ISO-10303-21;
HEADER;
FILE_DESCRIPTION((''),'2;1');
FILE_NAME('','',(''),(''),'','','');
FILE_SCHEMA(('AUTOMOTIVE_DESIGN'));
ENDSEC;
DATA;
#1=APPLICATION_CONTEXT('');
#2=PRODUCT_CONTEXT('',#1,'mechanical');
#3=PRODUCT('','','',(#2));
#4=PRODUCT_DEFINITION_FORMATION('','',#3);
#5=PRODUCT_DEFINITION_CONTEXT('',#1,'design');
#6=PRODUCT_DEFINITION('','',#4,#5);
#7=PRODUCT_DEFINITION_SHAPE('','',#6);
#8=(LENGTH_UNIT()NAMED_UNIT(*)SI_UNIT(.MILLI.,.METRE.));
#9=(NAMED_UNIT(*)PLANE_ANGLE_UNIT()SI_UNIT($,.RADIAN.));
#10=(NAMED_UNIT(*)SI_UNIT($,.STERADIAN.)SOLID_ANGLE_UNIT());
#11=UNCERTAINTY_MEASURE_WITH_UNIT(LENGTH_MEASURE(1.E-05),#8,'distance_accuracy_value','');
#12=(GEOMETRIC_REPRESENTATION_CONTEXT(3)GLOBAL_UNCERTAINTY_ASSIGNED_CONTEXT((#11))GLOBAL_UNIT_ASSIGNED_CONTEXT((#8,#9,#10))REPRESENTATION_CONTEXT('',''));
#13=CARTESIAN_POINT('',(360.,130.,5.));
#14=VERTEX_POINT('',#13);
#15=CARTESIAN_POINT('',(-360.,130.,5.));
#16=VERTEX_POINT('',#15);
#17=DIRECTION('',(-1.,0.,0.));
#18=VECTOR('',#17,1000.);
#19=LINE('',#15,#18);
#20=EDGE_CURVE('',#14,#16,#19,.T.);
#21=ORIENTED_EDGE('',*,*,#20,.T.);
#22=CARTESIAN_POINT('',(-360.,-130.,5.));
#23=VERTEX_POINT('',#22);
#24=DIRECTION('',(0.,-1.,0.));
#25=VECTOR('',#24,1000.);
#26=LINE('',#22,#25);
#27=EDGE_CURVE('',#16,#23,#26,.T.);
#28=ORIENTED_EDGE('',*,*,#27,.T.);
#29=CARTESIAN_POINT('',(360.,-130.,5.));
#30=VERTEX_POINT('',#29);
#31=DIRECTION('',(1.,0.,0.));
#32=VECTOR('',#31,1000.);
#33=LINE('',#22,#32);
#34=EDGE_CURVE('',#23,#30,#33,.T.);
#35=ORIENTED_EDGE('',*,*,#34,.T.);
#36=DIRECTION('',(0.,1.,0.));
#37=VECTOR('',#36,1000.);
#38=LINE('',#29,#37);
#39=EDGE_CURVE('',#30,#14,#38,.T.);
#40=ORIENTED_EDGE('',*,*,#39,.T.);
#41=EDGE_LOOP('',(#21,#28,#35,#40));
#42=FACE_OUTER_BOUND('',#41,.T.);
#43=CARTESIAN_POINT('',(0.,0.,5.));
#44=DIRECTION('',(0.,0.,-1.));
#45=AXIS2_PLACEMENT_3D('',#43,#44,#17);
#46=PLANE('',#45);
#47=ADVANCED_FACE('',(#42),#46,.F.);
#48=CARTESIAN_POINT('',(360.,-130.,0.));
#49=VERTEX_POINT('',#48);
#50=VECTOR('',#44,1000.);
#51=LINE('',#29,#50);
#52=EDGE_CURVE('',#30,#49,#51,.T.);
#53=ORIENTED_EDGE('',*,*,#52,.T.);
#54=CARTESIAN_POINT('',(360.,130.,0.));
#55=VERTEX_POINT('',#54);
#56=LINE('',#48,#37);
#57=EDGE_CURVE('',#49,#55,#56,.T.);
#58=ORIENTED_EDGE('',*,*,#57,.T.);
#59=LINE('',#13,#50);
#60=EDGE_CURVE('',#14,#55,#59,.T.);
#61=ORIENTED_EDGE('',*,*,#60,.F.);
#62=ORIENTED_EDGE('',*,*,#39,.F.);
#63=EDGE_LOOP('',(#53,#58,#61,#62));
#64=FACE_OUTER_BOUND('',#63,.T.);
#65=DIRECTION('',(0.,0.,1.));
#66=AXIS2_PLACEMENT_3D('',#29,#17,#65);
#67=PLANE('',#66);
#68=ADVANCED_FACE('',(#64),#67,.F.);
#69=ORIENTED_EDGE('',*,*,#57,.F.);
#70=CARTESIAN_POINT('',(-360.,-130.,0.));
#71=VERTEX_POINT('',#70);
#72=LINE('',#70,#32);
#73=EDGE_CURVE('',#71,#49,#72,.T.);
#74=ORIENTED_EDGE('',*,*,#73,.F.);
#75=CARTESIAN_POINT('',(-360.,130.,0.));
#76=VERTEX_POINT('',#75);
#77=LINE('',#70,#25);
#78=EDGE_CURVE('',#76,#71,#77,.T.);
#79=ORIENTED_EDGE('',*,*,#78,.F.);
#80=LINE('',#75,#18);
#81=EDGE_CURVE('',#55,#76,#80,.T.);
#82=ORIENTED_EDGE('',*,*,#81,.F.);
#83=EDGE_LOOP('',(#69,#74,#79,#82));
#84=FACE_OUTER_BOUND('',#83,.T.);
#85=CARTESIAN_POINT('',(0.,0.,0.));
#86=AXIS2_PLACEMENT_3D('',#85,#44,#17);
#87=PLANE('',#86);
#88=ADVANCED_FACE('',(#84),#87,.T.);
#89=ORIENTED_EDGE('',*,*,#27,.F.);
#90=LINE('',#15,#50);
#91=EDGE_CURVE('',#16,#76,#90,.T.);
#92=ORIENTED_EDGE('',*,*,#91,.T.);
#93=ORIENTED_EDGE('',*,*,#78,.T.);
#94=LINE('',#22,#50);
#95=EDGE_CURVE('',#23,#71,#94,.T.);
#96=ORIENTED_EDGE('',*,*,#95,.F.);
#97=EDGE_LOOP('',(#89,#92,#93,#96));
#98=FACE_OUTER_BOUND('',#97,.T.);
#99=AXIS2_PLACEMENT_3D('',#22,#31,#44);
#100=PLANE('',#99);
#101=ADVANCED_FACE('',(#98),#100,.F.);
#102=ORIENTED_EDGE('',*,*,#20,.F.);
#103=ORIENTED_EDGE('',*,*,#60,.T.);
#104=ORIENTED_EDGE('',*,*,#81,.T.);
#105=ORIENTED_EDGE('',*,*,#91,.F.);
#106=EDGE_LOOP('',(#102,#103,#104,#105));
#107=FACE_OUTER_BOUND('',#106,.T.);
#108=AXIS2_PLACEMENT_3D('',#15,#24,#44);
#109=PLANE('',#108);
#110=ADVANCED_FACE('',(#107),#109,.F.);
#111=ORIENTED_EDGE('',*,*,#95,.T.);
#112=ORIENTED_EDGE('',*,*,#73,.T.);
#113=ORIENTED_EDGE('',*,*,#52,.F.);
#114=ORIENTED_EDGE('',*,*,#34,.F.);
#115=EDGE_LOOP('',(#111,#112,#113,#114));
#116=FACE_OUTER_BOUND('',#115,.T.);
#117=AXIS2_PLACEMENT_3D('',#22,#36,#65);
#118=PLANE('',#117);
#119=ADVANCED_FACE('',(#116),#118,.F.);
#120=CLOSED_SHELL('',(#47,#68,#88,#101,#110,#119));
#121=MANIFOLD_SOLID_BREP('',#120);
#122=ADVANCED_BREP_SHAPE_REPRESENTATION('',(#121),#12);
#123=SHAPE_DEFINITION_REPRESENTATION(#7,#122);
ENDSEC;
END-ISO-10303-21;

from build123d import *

# Parameters (mm, degrees)
SKETCH_1_W      = 720
SKETCH_1_H      = 260
EXTRUDE_1_DEPTH = 5


with BuildPart() as part:
    # 草图1 → 凸台-拉伸1 (new body)
    with BuildSketch(Plane.XY):
        Rectangle(SKETCH_1_W, SKETCH_1_H)
    extrude(amount=EXTRUDE_1_DEPTH)


solid = part.part
